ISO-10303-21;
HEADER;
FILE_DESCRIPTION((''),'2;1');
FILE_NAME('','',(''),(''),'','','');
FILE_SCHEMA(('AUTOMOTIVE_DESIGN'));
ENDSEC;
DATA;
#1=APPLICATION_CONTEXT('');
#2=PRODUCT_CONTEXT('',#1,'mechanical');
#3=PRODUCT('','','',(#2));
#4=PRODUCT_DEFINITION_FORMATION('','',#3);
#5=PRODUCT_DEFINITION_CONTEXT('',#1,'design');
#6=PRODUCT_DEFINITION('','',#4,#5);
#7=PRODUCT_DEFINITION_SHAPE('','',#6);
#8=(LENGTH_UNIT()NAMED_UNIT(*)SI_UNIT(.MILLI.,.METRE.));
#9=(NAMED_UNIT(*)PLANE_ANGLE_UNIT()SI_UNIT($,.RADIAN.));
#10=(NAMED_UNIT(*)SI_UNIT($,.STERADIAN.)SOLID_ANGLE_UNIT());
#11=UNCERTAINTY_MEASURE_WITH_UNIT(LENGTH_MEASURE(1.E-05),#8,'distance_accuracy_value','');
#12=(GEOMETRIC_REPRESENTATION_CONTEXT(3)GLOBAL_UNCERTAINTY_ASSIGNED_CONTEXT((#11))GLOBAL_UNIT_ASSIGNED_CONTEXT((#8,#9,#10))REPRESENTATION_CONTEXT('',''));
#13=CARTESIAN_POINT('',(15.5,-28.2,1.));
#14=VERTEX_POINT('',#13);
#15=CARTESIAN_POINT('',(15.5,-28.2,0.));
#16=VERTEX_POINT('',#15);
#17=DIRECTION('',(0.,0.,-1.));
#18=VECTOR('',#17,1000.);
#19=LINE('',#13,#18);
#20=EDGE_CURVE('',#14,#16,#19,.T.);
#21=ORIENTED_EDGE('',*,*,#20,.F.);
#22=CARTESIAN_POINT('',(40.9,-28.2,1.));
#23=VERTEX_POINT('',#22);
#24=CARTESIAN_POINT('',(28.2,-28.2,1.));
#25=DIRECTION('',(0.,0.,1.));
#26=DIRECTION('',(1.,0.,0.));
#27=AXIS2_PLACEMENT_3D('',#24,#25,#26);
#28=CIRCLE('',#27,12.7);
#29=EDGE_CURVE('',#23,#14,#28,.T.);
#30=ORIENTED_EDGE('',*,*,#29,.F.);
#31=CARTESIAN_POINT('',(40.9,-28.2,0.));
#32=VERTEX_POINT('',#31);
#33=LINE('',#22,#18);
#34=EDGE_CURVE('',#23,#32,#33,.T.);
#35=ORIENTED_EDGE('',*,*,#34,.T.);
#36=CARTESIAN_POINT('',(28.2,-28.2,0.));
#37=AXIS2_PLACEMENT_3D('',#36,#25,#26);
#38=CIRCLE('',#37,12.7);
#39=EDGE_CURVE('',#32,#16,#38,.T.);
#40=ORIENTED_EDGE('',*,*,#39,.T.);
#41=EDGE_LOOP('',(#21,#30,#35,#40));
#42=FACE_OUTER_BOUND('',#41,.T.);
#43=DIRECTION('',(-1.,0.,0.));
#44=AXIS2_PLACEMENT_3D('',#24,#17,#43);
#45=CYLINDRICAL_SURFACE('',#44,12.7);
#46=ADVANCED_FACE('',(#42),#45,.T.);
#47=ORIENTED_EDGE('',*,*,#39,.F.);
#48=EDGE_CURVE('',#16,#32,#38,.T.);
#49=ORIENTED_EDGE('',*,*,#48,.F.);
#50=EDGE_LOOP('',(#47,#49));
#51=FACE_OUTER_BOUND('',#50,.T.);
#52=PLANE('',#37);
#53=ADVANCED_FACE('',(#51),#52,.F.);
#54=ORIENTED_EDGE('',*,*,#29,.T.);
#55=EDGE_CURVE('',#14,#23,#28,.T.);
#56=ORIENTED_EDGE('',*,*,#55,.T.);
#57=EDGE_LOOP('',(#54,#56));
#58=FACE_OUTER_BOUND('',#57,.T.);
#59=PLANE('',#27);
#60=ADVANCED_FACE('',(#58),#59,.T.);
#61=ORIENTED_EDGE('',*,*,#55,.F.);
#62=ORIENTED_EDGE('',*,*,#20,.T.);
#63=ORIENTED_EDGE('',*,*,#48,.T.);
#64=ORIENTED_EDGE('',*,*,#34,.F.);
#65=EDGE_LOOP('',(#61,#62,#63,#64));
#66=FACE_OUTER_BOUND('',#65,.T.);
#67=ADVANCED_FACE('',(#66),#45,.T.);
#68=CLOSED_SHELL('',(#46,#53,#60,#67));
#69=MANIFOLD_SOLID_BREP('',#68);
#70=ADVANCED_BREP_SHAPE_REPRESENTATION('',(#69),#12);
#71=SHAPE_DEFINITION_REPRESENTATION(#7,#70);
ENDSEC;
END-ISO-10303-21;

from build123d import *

# Parameters (mm, degrees)
SKETCH1_R           = 12.7
BOSS_EXTRUDE1_DEPTH = 1


with BuildPart() as part:
    # Sketch1 → Boss-Extrude1 (new body)
    with BuildSketch(Plane.XY):
        with Locations((28.2, -28.2)):
            Circle(SKETCH1_R)
    extrude(amount=BOSS_EXTRUDE1_DEPTH)


solid = part.part
